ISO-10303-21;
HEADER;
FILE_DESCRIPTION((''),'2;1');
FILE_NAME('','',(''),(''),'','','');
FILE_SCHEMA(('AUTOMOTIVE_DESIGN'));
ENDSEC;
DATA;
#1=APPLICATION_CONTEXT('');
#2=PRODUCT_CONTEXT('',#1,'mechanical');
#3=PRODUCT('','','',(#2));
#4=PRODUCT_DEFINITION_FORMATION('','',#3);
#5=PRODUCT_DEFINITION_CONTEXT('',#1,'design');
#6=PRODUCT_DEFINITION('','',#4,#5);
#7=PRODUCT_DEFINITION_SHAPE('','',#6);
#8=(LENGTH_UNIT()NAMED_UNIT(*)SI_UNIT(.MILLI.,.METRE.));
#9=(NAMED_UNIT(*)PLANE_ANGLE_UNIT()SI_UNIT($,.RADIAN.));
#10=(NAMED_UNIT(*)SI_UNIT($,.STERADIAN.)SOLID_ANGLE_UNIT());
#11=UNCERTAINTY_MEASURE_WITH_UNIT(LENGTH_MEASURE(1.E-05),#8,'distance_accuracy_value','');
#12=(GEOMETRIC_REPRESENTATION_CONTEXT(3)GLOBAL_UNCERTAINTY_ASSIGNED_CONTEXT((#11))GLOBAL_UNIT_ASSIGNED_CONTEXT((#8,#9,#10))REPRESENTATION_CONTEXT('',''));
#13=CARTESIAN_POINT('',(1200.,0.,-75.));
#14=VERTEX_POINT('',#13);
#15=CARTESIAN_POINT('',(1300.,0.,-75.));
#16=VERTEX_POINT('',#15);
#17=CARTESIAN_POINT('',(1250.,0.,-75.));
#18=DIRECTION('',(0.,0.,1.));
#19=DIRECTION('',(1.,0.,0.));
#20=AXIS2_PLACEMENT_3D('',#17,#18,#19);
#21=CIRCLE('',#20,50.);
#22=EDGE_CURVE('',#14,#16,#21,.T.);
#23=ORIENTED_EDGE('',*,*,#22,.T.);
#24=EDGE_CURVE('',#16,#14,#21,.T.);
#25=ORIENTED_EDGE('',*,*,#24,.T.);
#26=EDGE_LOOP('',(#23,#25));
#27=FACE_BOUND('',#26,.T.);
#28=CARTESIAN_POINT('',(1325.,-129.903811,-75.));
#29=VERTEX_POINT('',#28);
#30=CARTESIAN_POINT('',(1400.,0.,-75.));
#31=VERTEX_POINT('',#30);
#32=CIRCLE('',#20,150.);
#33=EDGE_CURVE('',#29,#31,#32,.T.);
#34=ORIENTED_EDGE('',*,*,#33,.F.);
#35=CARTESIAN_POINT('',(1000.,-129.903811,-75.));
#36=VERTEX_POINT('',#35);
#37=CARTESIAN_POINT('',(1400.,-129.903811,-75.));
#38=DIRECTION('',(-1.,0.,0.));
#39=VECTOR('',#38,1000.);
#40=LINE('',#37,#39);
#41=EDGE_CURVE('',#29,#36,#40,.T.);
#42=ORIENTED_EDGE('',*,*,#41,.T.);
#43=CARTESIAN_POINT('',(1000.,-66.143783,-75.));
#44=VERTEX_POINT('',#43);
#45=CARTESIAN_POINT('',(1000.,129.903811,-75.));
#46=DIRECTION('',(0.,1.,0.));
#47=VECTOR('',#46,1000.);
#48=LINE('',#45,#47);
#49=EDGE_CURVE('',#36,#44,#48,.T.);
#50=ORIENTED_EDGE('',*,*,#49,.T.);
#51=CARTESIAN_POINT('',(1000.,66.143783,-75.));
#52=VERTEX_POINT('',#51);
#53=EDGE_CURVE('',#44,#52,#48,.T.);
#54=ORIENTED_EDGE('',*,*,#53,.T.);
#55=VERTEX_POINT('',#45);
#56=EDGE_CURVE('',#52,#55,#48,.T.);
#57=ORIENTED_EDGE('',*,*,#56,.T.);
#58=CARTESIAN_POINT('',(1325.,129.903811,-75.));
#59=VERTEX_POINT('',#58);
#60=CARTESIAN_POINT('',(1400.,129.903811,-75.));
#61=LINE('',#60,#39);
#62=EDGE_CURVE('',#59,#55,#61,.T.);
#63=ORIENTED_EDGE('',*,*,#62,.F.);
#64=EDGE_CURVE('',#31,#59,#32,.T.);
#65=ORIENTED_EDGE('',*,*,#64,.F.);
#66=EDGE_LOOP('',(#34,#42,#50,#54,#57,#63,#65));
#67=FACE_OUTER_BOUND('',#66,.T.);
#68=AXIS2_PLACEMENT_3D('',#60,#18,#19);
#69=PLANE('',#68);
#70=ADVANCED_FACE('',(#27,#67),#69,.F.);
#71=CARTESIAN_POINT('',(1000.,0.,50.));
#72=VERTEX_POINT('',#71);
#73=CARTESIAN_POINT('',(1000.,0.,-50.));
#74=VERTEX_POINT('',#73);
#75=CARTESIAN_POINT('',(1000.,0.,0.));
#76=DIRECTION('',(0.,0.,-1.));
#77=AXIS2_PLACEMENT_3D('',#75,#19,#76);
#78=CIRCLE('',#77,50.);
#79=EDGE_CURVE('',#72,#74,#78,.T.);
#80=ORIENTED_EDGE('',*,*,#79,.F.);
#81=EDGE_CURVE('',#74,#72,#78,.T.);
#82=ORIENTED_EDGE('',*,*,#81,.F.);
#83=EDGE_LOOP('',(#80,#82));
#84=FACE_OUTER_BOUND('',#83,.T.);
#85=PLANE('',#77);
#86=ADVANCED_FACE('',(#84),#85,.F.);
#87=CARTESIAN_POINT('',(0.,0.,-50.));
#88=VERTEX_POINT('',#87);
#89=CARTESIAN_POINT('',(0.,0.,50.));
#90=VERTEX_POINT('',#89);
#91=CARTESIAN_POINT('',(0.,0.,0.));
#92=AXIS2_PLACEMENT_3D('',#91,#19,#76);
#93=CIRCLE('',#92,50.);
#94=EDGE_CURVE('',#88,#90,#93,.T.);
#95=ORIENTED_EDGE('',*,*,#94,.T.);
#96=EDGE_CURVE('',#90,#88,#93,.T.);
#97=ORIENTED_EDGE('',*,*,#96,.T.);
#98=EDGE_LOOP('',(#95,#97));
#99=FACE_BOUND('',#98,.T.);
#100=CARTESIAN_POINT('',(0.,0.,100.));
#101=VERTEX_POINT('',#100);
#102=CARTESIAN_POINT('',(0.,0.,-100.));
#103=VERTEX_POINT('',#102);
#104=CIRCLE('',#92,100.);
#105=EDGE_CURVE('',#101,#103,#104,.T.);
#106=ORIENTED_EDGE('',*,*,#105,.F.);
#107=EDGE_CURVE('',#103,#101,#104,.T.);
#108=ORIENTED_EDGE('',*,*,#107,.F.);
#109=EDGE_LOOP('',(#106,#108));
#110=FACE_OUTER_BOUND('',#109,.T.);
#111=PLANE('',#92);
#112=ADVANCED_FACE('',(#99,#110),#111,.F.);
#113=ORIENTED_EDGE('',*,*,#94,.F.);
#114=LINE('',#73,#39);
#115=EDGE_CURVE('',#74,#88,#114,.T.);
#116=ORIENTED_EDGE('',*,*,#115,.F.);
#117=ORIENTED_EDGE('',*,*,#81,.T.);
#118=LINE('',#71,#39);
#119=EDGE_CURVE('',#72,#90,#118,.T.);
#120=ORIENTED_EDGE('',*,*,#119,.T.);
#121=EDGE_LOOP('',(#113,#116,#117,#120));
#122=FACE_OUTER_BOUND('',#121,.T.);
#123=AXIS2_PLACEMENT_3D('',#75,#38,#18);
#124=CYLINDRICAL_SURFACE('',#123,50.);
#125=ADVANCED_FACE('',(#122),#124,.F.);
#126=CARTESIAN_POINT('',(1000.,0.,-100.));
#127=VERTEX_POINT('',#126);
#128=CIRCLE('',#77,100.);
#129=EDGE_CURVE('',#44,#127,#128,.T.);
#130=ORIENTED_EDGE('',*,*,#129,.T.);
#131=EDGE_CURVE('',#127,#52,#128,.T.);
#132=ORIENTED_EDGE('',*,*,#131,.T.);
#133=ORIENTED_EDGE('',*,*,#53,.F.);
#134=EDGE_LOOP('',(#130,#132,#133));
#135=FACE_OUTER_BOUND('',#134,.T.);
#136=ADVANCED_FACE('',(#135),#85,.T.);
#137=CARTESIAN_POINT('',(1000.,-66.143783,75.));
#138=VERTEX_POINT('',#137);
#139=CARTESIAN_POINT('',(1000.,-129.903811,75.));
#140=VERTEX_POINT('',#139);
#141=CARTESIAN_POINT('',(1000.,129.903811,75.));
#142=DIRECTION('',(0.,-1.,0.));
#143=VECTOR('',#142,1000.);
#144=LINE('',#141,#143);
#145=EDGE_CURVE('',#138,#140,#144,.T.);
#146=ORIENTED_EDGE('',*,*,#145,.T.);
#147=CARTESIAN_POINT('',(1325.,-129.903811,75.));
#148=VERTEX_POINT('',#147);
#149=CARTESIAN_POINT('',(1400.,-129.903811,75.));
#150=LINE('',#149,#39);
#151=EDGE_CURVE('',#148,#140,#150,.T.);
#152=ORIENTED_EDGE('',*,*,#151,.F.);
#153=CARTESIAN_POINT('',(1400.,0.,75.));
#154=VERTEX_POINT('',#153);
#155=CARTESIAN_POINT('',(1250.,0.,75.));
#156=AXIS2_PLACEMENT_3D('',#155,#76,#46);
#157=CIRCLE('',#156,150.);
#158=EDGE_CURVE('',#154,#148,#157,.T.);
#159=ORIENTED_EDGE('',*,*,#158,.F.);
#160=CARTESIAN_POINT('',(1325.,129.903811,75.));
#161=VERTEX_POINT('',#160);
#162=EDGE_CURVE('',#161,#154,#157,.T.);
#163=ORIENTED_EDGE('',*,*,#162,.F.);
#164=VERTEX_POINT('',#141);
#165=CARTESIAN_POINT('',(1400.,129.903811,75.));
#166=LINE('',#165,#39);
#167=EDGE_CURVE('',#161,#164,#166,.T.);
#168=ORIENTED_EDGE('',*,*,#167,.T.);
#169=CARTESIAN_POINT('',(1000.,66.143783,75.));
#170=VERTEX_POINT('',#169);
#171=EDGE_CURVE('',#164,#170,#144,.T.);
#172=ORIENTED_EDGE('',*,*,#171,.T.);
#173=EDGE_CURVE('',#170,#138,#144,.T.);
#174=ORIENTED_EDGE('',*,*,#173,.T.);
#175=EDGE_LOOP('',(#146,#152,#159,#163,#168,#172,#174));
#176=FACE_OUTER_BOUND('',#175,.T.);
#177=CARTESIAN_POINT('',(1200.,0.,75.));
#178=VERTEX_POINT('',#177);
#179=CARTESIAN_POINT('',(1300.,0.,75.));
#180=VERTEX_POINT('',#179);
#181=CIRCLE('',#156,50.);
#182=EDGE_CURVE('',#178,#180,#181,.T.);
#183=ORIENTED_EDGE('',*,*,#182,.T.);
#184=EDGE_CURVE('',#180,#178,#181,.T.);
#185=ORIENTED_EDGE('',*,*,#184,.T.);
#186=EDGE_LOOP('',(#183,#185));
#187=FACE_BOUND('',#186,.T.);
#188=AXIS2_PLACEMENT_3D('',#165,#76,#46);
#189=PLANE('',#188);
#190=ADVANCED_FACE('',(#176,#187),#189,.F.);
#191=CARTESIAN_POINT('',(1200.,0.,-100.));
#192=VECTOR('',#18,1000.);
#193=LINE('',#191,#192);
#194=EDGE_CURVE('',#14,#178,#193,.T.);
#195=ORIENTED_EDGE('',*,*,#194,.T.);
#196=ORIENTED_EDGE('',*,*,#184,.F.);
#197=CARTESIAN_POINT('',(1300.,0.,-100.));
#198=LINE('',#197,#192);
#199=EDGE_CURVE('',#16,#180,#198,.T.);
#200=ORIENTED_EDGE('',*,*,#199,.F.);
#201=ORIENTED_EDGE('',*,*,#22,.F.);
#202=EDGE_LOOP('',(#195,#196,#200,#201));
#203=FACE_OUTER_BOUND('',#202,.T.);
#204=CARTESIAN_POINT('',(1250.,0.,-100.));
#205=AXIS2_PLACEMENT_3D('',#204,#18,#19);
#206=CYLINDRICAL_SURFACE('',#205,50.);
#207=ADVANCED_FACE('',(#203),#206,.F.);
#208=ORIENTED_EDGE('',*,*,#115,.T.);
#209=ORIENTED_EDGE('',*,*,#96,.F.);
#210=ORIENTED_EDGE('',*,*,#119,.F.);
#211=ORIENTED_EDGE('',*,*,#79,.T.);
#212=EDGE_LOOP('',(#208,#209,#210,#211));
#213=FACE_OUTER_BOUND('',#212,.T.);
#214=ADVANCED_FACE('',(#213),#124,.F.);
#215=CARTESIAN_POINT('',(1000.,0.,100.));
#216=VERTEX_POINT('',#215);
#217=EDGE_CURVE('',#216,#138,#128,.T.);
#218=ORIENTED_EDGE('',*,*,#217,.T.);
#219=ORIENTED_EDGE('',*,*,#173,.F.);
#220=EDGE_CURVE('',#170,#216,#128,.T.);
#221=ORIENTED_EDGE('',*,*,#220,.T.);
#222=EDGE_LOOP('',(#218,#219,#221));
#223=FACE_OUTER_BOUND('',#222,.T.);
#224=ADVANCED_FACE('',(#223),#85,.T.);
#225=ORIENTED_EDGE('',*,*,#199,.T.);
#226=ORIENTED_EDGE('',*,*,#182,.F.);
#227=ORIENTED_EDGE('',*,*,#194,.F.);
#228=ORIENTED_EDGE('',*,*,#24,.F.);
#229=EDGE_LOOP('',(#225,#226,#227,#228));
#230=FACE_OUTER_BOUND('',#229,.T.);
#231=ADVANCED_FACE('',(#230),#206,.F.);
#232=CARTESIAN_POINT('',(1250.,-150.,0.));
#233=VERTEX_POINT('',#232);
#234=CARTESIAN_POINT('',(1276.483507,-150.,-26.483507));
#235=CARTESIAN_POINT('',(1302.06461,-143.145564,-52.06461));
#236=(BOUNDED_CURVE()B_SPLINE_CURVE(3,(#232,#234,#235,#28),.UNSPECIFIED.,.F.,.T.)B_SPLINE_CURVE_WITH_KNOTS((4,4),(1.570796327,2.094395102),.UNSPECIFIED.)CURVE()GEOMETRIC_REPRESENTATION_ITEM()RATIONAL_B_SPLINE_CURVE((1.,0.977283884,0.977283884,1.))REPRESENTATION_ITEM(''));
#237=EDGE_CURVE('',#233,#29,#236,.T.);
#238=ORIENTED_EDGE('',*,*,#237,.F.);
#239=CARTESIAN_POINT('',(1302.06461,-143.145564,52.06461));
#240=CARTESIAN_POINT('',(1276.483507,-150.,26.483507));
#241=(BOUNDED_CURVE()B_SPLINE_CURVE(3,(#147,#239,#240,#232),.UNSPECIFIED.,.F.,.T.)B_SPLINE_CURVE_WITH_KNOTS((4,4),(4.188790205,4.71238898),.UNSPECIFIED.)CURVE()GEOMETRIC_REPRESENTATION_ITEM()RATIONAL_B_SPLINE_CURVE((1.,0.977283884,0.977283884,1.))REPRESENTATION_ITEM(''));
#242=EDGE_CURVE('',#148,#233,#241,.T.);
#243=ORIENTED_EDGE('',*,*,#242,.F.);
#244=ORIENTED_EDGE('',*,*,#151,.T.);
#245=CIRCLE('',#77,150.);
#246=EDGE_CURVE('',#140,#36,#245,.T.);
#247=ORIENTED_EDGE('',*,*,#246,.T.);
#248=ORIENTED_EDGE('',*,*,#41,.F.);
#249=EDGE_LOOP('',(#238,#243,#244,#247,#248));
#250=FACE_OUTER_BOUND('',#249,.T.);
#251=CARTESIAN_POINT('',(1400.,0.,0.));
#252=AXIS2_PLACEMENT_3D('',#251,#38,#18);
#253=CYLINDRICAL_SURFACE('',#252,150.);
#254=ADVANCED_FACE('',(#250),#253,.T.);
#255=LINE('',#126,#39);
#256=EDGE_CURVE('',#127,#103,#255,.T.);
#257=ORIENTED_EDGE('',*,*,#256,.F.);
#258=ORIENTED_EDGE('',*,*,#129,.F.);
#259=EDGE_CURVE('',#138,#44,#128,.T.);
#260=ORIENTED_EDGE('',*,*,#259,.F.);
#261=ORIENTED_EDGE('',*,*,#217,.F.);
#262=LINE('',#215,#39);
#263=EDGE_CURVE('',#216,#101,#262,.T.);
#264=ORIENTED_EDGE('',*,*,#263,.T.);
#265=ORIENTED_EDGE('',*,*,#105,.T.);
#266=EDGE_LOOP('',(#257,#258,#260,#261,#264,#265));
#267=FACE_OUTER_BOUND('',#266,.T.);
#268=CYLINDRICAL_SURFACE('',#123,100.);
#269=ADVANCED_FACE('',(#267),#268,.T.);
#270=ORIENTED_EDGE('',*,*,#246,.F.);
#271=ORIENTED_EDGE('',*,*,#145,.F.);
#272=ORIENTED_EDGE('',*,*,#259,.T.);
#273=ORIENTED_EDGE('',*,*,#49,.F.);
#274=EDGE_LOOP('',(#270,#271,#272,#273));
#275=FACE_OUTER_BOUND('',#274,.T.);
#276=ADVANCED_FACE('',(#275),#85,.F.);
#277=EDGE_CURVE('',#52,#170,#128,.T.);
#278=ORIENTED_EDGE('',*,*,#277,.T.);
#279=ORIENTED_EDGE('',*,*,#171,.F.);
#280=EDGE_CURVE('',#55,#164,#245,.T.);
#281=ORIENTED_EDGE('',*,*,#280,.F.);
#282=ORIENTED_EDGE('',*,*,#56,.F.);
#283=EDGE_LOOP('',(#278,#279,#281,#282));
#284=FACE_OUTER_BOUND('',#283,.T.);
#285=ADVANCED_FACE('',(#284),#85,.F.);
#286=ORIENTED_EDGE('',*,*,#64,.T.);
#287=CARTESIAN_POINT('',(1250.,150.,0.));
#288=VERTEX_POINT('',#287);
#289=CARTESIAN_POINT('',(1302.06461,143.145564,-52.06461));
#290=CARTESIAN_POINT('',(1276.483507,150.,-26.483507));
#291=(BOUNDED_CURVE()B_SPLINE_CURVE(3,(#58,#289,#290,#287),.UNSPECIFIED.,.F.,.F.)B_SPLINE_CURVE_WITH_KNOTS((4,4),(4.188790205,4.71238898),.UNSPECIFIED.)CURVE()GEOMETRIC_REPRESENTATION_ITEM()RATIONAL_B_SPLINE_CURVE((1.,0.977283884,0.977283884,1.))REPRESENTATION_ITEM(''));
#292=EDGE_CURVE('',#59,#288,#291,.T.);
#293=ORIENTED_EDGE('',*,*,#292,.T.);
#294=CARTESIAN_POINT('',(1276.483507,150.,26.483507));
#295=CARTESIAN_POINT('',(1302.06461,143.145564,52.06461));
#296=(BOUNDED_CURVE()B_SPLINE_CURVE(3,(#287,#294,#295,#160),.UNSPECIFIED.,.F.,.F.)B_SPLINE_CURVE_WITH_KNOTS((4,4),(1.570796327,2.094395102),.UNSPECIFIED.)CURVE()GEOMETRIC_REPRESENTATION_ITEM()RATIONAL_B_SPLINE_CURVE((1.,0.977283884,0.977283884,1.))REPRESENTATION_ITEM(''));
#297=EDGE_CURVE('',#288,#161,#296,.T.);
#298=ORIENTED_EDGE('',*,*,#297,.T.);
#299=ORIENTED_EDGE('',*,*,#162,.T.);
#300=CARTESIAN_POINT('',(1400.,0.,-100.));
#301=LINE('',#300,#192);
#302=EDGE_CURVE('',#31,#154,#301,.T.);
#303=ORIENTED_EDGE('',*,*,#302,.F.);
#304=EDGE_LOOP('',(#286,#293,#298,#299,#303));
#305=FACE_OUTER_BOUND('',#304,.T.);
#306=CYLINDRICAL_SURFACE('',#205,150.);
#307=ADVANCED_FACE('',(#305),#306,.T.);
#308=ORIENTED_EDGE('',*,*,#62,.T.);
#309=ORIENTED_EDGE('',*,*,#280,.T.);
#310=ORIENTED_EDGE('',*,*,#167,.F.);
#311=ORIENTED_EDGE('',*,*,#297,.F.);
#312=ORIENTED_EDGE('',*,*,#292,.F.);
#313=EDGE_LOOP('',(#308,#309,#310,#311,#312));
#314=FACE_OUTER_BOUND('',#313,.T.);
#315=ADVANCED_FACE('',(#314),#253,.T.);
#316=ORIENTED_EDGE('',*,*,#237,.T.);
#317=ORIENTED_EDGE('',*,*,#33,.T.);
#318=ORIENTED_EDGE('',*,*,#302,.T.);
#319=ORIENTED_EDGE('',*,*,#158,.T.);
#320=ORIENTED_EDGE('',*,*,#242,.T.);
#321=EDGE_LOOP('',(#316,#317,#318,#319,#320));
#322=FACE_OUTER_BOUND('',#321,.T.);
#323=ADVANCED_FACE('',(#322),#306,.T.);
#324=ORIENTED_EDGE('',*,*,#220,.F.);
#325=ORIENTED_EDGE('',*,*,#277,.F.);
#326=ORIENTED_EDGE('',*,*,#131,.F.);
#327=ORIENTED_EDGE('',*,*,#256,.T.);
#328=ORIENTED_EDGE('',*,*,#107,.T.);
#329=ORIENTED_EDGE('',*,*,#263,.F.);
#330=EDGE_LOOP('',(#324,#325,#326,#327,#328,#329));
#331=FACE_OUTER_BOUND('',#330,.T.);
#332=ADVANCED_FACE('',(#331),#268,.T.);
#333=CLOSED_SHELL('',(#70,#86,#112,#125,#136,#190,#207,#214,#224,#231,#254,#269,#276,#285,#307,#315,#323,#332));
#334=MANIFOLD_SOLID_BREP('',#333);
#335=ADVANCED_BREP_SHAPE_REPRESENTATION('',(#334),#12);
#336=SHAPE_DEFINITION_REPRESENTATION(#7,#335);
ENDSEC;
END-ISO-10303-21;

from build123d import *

# Parameters (mm, degrees)
SKETCH1_R               = 100
SKETCH1_R_2             = 50
BOSS_EXTRUDE1_DEPTH     = 1000
BOSS_EXTRUDE2_DEPTH     = 400
CUT_EXTRUDE2_DEPTH      = 1419.846362366
CUT_EXTRUDE2_DEPTH_BACK = 1419.846362366
CUT_EXTRUDE3_DEPTH      = 1419.846362366
CUT_EXTRUDE3_DEPTH_BACK = 1419.846362366
SKETCH_4_5_2_R          = 50


with BuildPart() as part:
    # Sketch1 → Boss-Extrude1 (new body)
    with BuildSketch(Plane(origin=(0, 0, 0), x_dir=(0, 0, -1), z_dir=(1, 0, 0))):
        Circle(SKETCH1_R)
        Circle(SKETCH1_R_2, mode=Mode.SUBTRACT)
    extrude(amount=BOSS_EXTRUDE1_DEPTH)

    # Sketch3 → Boss-Extrude2 (add)
    with BuildSketch(Plane(origin=(1000, 0, 0), x_dir=(0, 0, -1), z_dir=(1, 0, 0))):
        with BuildLine():
            Line((-75, 129.903810568), (-75, -129.903810568))
            ThreePointArc((-75, -129.903810568), (0, -150), (75, -129.903810568))
            Line((75, -129.903810568), (75, 129.903810568))
            ThreePointArc((75, 129.903810568), (0, 150), (-75, 129.903810568))
        make_face()
    extrude(amount=BOSS_EXTRUDE2_DEPTH)

    # Sketch 4_5 → Cut-Extrude2 (cut, two sides: drawn at the far end of the back side and taken through both)
    with BuildSketch(Plane.XY.offset(75).offset(-CUT_EXTRUDE2_DEPTH_BACK)):
        with BuildLine():
            Line((1250, 150), (1455.357524725, 150))
            Line((1455.357524725, 150), (1455.357524725, -150))
            Line((1455.357524725, -150), (1250, -150))
            ThreePointArc((1250, -150), (1400, 0), (1250, 150))
        make_face()
    extrude(amount=CUT_EXTRUDE2_DEPTH + CUT_EXTRUDE2_DEPTH_BACK, mode=Mode.SUBTRACT)

    # Sketch 4_5 2 → Cut-Extrude3 (cut, two sides: drawn at the far end of the back side and taken through both)
    with BuildSketch(Plane.XY.offset(75).offset(-CUT_EXTRUDE3_DEPTH_BACK)):
        with Locations((1250, 0)):
            Circle(SKETCH_4_5_2_R)
    extrude(amount=CUT_EXTRUDE3_DEPTH + CUT_EXTRUDE3_DEPTH_BACK, mode=Mode.SUBTRACT)


solid = part.part
